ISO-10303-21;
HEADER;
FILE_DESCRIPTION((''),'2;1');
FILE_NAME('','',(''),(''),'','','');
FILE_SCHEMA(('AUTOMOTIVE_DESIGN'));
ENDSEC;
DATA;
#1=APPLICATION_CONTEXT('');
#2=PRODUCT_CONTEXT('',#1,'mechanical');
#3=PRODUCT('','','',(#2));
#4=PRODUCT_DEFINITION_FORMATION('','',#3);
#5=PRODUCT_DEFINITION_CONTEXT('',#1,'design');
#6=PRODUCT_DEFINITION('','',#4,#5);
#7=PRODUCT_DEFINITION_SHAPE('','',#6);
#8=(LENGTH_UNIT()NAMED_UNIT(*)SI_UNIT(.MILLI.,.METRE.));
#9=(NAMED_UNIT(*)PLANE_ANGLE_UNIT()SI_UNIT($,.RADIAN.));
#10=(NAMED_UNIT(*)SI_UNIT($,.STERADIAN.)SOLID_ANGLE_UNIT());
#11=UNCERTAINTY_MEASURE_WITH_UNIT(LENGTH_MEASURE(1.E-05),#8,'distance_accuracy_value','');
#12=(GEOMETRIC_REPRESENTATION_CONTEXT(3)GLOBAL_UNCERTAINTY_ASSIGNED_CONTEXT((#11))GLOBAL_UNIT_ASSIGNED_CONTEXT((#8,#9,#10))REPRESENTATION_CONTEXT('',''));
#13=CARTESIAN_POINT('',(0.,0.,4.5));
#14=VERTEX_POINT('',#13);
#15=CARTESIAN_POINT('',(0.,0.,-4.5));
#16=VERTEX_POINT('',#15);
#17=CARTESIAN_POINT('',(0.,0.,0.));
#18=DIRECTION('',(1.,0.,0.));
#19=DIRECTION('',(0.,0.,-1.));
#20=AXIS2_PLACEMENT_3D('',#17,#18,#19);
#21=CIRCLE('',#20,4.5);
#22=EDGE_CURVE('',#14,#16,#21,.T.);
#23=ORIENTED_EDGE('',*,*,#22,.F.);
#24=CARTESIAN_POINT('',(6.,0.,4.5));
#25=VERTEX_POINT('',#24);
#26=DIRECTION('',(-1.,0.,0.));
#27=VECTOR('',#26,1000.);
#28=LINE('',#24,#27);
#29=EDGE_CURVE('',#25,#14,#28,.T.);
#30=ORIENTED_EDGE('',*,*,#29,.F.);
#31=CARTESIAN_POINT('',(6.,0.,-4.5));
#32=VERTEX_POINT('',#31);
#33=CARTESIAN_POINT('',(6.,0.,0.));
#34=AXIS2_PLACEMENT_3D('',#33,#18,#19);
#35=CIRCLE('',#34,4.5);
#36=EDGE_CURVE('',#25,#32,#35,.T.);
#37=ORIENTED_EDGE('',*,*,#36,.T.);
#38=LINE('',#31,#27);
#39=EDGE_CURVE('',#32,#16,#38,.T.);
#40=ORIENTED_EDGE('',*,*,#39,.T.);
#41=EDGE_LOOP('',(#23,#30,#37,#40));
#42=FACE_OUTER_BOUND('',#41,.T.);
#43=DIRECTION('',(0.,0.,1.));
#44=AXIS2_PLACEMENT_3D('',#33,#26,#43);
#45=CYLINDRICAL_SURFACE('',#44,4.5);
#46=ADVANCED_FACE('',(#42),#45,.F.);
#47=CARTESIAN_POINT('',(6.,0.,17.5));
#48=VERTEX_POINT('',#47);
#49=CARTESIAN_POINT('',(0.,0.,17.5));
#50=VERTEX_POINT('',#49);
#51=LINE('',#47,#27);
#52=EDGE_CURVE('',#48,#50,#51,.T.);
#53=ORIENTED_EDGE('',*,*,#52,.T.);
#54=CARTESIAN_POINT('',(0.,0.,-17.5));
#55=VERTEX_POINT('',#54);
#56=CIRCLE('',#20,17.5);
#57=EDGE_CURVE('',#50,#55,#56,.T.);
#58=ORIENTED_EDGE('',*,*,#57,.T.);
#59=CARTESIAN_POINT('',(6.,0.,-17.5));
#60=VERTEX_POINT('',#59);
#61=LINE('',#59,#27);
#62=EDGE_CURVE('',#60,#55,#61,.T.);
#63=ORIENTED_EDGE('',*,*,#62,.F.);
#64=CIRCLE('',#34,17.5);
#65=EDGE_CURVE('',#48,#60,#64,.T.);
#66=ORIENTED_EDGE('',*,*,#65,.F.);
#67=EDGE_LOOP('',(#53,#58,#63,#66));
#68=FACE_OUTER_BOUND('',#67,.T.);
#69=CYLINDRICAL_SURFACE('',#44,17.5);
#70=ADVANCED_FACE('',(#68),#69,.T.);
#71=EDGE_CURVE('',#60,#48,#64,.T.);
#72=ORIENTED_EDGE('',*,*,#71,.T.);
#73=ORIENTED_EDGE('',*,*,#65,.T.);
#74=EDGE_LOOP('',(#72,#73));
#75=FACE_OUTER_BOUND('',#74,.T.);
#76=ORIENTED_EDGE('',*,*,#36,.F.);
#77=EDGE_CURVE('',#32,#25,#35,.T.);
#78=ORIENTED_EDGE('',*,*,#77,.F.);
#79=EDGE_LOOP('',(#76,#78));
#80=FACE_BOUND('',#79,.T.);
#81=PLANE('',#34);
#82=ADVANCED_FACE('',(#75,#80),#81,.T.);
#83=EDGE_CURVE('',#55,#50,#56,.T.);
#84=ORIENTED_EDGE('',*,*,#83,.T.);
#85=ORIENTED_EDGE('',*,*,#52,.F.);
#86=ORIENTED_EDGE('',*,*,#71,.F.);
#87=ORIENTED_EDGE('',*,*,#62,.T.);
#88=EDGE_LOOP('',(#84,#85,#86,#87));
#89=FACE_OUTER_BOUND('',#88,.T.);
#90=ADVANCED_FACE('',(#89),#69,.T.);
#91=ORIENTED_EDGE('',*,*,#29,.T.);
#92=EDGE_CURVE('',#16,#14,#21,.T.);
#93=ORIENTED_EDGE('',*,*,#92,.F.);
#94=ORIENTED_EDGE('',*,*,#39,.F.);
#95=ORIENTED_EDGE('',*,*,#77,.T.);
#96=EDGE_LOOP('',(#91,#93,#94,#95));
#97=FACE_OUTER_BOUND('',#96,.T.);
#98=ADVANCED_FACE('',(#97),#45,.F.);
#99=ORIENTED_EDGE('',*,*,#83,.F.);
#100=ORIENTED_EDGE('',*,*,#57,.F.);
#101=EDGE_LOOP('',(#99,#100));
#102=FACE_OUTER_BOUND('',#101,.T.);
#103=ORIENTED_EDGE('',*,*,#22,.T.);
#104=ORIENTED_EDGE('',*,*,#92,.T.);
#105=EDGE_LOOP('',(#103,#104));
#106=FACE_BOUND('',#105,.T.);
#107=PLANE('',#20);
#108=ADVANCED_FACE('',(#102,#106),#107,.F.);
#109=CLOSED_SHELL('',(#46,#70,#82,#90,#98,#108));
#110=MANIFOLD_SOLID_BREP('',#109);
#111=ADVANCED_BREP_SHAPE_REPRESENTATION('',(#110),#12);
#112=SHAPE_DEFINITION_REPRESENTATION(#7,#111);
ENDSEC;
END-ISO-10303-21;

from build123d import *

# Parameters (mm, degrees)
SKETCH_1_R      = 17.5
SKETCH_1_R_2    = 4.5
EXTRUDE_1_DEPTH = 6


with BuildPart() as part:
    # 草图1 → 凸台-拉伸1 (new body)
    with BuildSketch(Plane(origin=(0, 0, 0), x_dir=(0, 0, -1), z_dir=(1, 0, 0))):
        Circle(SKETCH_1_R)
        Circle(SKETCH_1_R_2, mode=Mode.SUBTRACT)
    extrude(amount=EXTRUDE_1_DEPTH)


solid = part.part
